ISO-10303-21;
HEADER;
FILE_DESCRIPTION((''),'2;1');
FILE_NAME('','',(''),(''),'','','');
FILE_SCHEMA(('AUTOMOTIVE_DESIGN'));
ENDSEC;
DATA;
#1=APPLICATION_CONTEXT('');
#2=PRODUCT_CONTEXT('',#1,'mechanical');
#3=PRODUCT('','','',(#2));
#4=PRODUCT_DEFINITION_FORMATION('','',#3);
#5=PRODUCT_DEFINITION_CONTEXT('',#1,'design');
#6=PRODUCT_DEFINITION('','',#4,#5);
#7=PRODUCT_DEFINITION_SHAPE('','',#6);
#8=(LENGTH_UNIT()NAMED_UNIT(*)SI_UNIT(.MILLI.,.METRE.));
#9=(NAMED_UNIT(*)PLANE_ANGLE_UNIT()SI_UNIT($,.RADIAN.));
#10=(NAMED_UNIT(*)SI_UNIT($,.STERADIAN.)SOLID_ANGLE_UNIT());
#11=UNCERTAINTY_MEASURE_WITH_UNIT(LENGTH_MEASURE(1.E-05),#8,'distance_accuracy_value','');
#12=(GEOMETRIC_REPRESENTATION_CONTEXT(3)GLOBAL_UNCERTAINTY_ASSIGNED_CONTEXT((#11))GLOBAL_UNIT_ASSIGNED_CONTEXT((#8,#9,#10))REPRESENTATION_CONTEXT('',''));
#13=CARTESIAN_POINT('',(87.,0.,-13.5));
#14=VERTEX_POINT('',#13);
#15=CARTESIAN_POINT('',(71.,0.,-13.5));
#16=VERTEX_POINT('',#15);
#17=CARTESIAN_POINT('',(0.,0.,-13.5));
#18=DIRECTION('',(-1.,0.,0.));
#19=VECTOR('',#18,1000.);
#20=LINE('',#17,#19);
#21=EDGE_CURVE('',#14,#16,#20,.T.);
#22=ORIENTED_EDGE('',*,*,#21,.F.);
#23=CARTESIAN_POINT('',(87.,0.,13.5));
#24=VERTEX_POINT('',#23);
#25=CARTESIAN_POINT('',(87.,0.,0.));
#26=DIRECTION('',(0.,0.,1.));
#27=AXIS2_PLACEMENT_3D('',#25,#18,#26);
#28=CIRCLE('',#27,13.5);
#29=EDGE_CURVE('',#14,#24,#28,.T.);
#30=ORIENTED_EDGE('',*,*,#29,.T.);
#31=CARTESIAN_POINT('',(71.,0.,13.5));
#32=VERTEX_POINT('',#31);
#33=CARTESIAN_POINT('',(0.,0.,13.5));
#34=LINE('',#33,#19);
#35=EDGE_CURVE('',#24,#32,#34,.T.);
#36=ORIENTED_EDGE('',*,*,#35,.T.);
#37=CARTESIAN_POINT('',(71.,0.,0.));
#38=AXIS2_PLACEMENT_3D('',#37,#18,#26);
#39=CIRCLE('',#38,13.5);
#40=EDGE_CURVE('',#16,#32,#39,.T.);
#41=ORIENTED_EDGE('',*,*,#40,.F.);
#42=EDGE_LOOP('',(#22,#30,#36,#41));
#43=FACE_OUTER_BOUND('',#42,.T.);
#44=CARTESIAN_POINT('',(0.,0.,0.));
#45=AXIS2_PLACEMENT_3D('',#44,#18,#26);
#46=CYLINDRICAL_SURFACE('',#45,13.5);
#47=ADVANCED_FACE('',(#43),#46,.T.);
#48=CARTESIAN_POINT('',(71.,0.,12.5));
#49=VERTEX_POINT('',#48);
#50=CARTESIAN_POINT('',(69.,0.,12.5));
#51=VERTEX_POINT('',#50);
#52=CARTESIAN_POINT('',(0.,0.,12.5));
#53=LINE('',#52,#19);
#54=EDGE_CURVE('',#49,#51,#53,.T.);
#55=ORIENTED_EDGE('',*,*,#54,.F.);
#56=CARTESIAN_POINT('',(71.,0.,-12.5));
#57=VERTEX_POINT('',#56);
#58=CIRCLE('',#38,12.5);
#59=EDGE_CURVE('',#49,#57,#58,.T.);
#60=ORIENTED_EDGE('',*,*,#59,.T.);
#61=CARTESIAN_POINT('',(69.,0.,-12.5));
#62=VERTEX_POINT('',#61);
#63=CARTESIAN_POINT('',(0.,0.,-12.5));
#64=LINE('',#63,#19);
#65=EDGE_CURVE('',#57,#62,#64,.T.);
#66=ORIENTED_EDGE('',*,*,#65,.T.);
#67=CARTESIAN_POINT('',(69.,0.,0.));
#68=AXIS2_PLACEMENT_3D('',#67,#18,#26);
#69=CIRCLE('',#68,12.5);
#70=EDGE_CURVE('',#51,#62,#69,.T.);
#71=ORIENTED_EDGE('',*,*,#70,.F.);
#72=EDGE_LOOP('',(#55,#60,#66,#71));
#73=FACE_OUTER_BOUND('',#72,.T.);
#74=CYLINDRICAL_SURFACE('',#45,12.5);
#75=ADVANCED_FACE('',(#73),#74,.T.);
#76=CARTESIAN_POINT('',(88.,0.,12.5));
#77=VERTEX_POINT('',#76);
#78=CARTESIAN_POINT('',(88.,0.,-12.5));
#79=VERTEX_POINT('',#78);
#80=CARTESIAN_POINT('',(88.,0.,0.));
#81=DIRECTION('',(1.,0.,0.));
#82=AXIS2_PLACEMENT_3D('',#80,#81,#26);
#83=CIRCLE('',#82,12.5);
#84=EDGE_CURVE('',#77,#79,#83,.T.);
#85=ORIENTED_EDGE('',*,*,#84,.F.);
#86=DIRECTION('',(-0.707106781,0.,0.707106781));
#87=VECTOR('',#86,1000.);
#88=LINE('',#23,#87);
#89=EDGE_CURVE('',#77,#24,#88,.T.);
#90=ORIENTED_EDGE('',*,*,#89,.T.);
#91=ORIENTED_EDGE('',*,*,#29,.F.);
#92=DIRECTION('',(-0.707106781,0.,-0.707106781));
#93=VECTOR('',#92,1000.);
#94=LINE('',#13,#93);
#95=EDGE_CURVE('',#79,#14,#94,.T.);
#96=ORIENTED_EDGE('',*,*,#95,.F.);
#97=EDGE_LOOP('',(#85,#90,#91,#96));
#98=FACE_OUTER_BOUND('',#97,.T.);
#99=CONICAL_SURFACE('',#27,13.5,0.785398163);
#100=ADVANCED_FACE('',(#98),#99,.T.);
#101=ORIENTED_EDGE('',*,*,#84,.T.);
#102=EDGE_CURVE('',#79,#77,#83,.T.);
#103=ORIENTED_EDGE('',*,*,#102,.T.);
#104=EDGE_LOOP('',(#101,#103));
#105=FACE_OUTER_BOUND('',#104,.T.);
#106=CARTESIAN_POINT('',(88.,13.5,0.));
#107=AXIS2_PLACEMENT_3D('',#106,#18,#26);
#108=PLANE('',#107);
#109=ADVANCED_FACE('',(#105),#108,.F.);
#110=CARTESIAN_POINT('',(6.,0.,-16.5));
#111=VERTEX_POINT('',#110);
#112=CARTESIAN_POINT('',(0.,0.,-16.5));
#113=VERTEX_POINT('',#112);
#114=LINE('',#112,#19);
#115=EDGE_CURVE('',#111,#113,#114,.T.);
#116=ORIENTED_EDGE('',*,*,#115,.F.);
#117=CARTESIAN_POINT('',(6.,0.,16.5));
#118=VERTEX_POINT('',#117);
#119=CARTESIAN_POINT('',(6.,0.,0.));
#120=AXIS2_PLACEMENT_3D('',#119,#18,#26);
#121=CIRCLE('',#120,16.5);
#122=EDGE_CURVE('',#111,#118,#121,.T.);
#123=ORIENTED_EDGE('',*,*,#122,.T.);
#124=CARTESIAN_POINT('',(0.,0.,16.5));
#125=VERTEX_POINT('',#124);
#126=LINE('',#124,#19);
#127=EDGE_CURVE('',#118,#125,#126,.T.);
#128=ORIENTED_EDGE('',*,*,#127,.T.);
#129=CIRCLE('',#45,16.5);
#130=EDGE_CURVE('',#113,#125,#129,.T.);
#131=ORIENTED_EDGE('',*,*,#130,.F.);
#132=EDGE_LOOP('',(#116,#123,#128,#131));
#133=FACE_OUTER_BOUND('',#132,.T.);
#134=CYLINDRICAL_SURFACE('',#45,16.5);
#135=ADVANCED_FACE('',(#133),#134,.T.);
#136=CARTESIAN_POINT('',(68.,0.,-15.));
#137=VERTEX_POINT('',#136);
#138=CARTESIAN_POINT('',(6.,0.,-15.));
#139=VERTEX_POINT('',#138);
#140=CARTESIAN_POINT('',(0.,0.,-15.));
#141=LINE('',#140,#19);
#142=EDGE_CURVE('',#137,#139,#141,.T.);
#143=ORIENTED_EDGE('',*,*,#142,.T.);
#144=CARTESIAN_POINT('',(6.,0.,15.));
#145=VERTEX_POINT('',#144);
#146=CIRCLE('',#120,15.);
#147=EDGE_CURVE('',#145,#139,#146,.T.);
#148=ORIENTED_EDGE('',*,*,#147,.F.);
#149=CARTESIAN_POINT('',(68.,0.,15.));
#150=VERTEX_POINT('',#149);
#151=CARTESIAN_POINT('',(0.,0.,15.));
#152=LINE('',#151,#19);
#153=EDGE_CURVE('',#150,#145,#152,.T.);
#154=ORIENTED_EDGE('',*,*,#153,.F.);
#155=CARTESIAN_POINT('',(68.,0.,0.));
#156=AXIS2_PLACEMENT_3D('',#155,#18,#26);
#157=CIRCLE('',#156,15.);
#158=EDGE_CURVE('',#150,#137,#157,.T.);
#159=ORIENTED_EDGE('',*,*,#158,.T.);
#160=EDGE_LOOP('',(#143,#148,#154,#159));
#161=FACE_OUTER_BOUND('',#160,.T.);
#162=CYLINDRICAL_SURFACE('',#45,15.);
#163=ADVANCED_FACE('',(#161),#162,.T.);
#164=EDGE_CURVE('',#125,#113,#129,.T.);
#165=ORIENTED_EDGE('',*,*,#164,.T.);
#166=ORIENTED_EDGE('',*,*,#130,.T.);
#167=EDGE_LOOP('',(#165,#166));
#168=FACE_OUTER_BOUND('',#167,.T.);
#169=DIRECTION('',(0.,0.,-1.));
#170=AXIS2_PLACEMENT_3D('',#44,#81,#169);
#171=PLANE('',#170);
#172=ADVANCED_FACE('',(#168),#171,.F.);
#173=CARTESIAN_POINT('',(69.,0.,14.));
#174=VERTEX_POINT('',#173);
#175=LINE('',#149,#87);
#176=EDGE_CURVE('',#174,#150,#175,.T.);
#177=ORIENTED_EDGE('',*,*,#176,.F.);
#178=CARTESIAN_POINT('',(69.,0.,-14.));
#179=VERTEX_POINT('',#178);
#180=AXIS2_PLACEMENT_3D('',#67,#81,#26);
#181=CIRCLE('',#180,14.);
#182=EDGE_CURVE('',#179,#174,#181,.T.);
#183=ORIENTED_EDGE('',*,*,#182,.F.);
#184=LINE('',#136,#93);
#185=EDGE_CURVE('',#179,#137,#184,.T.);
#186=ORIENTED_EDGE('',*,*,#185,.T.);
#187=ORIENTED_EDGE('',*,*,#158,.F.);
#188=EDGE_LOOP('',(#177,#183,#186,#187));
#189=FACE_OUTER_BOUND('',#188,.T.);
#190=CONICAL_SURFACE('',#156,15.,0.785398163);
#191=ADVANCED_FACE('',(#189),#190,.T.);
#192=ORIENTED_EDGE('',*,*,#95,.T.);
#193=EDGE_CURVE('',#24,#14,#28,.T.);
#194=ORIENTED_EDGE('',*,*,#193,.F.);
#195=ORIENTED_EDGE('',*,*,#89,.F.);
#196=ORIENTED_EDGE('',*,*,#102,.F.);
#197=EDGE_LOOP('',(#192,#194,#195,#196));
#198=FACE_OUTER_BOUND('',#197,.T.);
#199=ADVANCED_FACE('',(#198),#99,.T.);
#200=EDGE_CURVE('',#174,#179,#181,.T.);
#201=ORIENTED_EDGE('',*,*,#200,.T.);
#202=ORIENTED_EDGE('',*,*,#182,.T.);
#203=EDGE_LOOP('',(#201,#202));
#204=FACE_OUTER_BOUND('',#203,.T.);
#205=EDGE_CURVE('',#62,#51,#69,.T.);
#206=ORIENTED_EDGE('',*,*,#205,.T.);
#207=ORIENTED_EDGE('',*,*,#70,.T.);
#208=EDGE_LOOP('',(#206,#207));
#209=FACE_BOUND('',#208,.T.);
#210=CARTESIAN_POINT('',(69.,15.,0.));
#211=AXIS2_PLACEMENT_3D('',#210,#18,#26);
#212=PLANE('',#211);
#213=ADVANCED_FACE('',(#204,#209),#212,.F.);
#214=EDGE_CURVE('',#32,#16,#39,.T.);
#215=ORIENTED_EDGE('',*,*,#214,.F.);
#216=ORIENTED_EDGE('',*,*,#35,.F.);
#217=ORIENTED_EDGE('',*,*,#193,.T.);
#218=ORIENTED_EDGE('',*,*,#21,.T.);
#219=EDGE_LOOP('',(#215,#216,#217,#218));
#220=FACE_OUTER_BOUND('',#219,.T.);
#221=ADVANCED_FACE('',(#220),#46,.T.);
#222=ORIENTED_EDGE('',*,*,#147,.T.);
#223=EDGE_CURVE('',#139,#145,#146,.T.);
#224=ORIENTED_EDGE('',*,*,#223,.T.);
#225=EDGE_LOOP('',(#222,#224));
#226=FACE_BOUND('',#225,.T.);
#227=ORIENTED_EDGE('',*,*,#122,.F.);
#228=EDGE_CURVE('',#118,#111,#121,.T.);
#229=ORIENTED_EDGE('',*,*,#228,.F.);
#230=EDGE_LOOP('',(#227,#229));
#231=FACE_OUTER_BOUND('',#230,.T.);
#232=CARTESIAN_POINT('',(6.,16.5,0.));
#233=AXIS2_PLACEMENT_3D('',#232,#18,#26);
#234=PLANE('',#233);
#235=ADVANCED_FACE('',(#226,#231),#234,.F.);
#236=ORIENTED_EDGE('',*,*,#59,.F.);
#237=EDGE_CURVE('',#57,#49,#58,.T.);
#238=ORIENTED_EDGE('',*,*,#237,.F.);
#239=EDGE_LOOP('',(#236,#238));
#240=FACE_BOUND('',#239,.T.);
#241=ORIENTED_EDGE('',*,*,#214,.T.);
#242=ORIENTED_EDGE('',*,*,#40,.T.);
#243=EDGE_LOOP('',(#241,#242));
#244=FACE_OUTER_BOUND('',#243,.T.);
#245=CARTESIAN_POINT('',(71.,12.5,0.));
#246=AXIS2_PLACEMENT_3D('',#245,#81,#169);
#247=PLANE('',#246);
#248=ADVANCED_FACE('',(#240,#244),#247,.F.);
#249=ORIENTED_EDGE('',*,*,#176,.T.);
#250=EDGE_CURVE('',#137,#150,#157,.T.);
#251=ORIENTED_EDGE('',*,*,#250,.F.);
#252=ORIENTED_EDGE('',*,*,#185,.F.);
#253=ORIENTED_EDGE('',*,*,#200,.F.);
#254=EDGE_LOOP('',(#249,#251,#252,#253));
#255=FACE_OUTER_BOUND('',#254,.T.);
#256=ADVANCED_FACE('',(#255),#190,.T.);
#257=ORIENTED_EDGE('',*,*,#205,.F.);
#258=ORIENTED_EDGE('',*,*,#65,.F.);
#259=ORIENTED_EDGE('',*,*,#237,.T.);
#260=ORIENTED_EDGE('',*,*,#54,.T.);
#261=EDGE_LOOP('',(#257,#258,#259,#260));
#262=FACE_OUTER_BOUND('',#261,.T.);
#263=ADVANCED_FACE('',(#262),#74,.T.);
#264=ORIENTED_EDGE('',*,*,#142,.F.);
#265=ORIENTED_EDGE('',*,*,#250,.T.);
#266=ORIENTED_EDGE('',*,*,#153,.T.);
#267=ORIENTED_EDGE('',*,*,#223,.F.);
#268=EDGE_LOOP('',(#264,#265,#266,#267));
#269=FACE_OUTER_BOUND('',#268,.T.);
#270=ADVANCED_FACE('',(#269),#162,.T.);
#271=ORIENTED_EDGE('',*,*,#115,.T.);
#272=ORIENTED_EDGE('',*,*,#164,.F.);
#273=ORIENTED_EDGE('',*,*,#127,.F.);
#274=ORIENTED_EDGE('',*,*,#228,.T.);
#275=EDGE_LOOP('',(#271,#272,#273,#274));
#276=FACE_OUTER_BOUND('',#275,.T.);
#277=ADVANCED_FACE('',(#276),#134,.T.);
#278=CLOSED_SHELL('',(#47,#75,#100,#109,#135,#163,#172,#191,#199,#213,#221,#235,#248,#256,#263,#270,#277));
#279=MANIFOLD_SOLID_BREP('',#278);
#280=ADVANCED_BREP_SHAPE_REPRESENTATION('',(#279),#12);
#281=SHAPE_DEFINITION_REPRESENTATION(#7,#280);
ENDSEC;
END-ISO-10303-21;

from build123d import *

# Parameters (mm, degrees)
CHAMFER_1_SIZE = 1


with BuildPart() as part:
    # 草图1 → 旋转1 (revolve)
    with BuildSketch(Plane.XY, mode=Mode.PRIVATE) as revolve_1_sk:
        Polygon((0, 0), (0, 16.5), (6, 16.5), (6, 15), (69, 15), (69, 12.5), (71, 12.5), (71, 13.5), (88, 13.5), (88, 0), align=None)
    revolve(revolve_1_sk.sketch.rotate(Axis((0, 0, 0), (1, 0, 0)), 90), axis=Axis((0, 0, 0), (1, 0, 0)))

    # 倒角1
    chamfer_1_edges = [part.edges().sort_by_distance(p)[0] for p in [
        (69, 0, -15),
        (88, 0, -13.5),
    ]]
    chamfer(chamfer_1_edges, length=CHAMFER_1_SIZE)


solid = part.part
